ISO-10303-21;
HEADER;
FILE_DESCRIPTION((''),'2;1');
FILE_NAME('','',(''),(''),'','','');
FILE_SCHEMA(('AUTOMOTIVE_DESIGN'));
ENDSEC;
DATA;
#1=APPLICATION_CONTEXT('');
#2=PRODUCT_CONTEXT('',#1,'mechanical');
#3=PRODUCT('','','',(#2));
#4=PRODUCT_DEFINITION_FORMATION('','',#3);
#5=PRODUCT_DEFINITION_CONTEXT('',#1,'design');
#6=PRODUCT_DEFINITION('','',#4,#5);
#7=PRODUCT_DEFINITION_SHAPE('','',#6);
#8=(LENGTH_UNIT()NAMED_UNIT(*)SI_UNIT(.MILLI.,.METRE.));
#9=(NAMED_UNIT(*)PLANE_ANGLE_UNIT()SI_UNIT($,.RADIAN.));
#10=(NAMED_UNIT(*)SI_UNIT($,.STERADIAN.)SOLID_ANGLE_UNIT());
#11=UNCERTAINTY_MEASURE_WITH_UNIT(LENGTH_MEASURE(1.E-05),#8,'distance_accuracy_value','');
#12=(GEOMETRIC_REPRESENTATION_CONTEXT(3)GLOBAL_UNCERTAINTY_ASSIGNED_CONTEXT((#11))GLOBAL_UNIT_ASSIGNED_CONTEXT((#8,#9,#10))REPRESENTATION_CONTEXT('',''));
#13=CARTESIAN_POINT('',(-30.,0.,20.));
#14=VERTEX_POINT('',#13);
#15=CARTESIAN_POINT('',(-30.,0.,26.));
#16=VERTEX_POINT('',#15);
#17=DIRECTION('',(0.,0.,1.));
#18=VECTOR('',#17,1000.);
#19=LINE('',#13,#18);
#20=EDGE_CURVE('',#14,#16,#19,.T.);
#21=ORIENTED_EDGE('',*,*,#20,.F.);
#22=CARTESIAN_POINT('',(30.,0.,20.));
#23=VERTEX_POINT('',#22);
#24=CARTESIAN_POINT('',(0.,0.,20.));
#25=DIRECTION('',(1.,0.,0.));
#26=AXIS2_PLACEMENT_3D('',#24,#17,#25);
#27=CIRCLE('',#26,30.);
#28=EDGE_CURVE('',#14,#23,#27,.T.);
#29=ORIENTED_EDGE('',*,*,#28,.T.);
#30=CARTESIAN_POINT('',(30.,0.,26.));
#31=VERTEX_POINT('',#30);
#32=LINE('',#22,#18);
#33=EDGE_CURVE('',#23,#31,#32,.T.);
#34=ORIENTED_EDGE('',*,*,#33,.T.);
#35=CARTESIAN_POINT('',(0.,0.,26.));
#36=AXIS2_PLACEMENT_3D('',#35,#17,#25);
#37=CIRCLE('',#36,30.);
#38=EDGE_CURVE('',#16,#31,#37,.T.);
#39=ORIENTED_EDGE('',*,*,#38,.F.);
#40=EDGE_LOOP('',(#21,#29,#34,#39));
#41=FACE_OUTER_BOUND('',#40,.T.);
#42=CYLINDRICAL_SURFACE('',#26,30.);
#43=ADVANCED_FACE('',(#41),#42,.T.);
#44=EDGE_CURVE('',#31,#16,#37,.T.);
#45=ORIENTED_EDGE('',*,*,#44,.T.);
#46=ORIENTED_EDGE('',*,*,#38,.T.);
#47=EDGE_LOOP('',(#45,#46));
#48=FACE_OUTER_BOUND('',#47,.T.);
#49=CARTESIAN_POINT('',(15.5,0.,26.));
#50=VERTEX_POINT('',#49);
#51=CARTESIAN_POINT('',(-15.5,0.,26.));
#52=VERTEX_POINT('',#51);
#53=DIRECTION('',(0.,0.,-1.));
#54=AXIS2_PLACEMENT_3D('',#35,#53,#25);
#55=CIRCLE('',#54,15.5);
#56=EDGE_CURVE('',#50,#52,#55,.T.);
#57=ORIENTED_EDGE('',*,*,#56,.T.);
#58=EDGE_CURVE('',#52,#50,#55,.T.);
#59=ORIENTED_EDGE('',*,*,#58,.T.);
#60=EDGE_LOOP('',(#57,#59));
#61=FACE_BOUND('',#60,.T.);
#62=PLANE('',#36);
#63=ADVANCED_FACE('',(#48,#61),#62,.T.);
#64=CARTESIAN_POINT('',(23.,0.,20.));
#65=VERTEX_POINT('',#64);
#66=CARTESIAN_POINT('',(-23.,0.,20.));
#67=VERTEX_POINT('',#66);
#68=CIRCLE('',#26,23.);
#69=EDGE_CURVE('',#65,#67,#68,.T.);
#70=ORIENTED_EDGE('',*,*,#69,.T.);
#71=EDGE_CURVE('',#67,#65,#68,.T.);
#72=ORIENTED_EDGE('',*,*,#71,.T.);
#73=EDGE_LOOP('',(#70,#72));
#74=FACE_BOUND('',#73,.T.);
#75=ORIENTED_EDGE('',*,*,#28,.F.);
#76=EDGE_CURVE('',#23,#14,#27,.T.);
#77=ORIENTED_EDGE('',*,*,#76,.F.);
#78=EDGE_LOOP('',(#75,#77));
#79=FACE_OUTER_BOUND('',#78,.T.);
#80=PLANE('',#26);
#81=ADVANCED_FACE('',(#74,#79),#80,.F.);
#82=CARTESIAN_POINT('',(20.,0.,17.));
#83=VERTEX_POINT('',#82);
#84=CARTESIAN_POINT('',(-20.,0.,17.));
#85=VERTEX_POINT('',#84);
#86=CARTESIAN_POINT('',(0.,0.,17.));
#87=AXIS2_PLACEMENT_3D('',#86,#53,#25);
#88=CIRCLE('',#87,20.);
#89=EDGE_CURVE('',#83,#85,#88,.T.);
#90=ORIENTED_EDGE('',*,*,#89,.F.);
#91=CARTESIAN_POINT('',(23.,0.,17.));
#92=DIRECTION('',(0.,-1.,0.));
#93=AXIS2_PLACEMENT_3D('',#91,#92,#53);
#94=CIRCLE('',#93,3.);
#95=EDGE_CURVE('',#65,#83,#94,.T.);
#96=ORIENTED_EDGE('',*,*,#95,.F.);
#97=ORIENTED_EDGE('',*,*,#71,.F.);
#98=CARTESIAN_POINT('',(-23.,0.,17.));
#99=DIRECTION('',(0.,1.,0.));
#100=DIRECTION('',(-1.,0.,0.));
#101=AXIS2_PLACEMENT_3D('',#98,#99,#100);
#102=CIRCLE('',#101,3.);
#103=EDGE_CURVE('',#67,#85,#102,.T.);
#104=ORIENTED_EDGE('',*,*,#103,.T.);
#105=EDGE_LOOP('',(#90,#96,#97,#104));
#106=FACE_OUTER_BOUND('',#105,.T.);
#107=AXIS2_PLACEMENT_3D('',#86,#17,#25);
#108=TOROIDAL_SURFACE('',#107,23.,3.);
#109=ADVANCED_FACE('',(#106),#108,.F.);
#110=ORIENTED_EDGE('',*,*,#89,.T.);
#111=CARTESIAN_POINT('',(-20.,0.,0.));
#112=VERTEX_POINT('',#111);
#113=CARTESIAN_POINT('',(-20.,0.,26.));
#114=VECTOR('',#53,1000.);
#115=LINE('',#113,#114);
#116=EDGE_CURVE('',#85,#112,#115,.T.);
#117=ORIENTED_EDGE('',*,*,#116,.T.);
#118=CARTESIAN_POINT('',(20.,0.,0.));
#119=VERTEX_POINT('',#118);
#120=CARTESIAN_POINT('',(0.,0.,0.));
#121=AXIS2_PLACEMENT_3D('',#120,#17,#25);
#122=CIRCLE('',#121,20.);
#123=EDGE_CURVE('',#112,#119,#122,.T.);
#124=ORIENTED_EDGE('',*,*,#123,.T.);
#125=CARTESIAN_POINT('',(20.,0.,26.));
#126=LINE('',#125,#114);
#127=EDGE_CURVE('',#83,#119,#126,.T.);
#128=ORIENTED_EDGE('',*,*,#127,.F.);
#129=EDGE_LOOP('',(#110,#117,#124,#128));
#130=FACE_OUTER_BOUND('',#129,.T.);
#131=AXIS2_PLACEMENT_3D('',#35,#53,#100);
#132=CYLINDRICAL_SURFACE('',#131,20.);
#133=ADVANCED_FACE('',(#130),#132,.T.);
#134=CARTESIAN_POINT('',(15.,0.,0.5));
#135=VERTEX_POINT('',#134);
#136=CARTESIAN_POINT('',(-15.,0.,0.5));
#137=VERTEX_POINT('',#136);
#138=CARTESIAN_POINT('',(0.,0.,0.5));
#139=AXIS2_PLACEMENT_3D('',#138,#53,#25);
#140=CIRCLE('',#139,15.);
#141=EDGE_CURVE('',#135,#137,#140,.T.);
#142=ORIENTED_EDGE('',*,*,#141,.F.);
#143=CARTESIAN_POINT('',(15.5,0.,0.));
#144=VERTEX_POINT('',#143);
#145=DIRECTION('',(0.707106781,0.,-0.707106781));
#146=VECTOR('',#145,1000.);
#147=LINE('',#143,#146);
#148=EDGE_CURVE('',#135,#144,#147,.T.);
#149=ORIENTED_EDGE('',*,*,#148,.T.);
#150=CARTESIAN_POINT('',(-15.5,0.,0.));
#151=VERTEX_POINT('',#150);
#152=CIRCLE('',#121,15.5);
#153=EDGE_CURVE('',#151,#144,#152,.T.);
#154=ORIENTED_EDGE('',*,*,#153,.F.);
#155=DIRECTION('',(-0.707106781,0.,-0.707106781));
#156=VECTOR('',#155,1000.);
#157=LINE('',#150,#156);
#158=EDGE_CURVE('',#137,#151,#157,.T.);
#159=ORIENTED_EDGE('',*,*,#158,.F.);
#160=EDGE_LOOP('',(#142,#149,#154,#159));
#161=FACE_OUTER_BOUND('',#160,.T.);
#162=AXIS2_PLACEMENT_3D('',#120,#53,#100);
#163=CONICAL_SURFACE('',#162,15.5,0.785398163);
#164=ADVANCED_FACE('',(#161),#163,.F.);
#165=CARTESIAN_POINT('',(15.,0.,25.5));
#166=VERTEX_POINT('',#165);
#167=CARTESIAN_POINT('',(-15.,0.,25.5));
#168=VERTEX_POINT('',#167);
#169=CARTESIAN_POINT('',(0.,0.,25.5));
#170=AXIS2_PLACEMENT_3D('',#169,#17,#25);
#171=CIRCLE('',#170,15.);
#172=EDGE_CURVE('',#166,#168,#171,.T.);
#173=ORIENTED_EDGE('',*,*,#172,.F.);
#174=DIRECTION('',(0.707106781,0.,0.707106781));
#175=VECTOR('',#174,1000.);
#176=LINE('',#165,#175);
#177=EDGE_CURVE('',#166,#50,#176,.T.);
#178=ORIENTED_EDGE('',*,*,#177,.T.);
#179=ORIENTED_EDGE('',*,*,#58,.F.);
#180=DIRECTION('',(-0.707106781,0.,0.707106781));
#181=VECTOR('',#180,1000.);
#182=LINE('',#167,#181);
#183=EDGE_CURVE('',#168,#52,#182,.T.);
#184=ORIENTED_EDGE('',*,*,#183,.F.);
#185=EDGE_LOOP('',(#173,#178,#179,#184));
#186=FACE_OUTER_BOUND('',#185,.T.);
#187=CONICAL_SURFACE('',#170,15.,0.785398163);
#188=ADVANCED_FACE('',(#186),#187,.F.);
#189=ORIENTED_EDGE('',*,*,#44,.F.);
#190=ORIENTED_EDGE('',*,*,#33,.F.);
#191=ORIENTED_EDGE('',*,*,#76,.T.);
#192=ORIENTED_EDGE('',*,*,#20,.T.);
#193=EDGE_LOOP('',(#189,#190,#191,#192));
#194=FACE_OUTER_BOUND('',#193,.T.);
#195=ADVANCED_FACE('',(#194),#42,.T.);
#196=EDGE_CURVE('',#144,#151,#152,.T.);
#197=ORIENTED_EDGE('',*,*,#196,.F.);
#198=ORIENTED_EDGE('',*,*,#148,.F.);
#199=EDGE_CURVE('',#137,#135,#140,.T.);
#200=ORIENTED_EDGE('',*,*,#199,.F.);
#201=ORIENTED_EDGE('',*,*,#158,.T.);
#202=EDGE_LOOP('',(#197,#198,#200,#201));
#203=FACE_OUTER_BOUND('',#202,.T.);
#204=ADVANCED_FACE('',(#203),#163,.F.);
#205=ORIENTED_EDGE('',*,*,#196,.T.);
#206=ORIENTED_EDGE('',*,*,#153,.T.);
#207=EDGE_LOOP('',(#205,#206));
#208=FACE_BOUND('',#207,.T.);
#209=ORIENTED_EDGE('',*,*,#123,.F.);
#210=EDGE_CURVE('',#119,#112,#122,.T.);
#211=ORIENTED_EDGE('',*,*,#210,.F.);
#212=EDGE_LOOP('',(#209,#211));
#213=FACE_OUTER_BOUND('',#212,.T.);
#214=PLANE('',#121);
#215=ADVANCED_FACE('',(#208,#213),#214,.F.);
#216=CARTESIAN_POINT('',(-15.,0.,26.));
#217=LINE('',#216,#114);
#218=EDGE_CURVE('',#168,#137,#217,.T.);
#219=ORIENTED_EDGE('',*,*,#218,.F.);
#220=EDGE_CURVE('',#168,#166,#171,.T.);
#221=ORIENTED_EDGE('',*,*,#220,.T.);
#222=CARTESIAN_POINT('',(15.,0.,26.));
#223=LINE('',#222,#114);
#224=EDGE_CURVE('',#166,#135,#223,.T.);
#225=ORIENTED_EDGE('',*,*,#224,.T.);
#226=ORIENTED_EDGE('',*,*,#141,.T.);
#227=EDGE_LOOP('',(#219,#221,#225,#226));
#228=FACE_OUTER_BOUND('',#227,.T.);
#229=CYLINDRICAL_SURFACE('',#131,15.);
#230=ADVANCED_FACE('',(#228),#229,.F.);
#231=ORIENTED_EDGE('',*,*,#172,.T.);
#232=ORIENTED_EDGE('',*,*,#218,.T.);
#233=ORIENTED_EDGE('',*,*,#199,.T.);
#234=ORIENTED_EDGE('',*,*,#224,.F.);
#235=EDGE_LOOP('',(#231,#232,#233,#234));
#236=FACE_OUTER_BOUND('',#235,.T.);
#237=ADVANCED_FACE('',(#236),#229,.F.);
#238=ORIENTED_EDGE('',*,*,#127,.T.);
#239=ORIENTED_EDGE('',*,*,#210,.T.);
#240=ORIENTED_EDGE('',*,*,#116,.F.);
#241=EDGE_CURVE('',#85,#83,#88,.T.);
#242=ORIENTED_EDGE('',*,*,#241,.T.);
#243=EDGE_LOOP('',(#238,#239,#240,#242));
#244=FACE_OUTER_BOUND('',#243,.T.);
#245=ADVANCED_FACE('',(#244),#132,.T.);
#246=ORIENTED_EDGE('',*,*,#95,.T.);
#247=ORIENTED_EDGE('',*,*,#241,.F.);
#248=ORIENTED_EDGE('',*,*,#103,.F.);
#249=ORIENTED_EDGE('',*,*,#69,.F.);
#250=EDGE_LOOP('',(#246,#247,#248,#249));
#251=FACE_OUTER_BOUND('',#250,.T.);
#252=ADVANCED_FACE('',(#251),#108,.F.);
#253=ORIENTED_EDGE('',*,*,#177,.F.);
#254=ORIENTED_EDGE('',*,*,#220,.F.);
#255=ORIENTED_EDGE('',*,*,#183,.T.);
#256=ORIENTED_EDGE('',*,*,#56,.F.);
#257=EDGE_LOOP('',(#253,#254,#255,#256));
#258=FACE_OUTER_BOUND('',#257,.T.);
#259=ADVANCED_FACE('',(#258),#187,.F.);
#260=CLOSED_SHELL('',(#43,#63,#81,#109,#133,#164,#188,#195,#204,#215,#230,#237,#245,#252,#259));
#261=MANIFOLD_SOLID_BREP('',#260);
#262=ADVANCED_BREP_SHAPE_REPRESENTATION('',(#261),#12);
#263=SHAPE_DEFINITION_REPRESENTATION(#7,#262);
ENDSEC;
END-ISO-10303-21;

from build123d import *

# Parameters (mm, degrees)
SKETCH1_R           = 20
SKETCH1_R_2         = 15
BOSS_EXTRUDE1_DEPTH = 26
BOSS_EXTRUDE2_START = -6
SKETCH2_R           = 30
SKETCH2_R_2         = 15
BOSS_EXTRUDE2_DEPTH = 6
FILLET1_R           = 3
CHAMFER2_SIZE       = 0.5


with BuildPart() as part:
    # Sketch1 → Boss-Extrude1 (new body)
    with BuildSketch(Plane.XY):
        with Locations(Location((0, 0, 0), (0, 0, 180))):
            Circle(SKETCH1_R)
        with Locations(Location((0, 0, 0), (0, 0, 180))):
            Circle(SKETCH1_R_2, mode=Mode.SUBTRACT)
    extrude(amount=BOSS_EXTRUDE1_DEPTH)

    # Sketch2 → Boss-Extrude2 (add)
    with BuildSketch(Plane.XY.offset(26).offset(BOSS_EXTRUDE2_START)):
        Circle(SKETCH2_R)
        with Locations(Location((0, 0, 0), (0, 0, 180))):
            Circle(SKETCH2_R_2, mode=Mode.SUBTRACT)
    extrude(amount=BOSS_EXTRUDE2_DEPTH)

    # Fillet1
    fillet1_edges = [part.edges().sort_by_distance(p)[0] for p in [
        (20, 0, 20),
    ]]
    fillet(fillet1_edges, radius=FILLET1_R)

    # Chamfer2
    chamfer2_edges = [part.edges().sort_by_distance(p)[0] for p in [
        (15, 0, 0),
        (15, 0, 26),
    ]]
    chamfer(chamfer2_edges, length=CHAMFER2_SIZE)


solid = part.part
